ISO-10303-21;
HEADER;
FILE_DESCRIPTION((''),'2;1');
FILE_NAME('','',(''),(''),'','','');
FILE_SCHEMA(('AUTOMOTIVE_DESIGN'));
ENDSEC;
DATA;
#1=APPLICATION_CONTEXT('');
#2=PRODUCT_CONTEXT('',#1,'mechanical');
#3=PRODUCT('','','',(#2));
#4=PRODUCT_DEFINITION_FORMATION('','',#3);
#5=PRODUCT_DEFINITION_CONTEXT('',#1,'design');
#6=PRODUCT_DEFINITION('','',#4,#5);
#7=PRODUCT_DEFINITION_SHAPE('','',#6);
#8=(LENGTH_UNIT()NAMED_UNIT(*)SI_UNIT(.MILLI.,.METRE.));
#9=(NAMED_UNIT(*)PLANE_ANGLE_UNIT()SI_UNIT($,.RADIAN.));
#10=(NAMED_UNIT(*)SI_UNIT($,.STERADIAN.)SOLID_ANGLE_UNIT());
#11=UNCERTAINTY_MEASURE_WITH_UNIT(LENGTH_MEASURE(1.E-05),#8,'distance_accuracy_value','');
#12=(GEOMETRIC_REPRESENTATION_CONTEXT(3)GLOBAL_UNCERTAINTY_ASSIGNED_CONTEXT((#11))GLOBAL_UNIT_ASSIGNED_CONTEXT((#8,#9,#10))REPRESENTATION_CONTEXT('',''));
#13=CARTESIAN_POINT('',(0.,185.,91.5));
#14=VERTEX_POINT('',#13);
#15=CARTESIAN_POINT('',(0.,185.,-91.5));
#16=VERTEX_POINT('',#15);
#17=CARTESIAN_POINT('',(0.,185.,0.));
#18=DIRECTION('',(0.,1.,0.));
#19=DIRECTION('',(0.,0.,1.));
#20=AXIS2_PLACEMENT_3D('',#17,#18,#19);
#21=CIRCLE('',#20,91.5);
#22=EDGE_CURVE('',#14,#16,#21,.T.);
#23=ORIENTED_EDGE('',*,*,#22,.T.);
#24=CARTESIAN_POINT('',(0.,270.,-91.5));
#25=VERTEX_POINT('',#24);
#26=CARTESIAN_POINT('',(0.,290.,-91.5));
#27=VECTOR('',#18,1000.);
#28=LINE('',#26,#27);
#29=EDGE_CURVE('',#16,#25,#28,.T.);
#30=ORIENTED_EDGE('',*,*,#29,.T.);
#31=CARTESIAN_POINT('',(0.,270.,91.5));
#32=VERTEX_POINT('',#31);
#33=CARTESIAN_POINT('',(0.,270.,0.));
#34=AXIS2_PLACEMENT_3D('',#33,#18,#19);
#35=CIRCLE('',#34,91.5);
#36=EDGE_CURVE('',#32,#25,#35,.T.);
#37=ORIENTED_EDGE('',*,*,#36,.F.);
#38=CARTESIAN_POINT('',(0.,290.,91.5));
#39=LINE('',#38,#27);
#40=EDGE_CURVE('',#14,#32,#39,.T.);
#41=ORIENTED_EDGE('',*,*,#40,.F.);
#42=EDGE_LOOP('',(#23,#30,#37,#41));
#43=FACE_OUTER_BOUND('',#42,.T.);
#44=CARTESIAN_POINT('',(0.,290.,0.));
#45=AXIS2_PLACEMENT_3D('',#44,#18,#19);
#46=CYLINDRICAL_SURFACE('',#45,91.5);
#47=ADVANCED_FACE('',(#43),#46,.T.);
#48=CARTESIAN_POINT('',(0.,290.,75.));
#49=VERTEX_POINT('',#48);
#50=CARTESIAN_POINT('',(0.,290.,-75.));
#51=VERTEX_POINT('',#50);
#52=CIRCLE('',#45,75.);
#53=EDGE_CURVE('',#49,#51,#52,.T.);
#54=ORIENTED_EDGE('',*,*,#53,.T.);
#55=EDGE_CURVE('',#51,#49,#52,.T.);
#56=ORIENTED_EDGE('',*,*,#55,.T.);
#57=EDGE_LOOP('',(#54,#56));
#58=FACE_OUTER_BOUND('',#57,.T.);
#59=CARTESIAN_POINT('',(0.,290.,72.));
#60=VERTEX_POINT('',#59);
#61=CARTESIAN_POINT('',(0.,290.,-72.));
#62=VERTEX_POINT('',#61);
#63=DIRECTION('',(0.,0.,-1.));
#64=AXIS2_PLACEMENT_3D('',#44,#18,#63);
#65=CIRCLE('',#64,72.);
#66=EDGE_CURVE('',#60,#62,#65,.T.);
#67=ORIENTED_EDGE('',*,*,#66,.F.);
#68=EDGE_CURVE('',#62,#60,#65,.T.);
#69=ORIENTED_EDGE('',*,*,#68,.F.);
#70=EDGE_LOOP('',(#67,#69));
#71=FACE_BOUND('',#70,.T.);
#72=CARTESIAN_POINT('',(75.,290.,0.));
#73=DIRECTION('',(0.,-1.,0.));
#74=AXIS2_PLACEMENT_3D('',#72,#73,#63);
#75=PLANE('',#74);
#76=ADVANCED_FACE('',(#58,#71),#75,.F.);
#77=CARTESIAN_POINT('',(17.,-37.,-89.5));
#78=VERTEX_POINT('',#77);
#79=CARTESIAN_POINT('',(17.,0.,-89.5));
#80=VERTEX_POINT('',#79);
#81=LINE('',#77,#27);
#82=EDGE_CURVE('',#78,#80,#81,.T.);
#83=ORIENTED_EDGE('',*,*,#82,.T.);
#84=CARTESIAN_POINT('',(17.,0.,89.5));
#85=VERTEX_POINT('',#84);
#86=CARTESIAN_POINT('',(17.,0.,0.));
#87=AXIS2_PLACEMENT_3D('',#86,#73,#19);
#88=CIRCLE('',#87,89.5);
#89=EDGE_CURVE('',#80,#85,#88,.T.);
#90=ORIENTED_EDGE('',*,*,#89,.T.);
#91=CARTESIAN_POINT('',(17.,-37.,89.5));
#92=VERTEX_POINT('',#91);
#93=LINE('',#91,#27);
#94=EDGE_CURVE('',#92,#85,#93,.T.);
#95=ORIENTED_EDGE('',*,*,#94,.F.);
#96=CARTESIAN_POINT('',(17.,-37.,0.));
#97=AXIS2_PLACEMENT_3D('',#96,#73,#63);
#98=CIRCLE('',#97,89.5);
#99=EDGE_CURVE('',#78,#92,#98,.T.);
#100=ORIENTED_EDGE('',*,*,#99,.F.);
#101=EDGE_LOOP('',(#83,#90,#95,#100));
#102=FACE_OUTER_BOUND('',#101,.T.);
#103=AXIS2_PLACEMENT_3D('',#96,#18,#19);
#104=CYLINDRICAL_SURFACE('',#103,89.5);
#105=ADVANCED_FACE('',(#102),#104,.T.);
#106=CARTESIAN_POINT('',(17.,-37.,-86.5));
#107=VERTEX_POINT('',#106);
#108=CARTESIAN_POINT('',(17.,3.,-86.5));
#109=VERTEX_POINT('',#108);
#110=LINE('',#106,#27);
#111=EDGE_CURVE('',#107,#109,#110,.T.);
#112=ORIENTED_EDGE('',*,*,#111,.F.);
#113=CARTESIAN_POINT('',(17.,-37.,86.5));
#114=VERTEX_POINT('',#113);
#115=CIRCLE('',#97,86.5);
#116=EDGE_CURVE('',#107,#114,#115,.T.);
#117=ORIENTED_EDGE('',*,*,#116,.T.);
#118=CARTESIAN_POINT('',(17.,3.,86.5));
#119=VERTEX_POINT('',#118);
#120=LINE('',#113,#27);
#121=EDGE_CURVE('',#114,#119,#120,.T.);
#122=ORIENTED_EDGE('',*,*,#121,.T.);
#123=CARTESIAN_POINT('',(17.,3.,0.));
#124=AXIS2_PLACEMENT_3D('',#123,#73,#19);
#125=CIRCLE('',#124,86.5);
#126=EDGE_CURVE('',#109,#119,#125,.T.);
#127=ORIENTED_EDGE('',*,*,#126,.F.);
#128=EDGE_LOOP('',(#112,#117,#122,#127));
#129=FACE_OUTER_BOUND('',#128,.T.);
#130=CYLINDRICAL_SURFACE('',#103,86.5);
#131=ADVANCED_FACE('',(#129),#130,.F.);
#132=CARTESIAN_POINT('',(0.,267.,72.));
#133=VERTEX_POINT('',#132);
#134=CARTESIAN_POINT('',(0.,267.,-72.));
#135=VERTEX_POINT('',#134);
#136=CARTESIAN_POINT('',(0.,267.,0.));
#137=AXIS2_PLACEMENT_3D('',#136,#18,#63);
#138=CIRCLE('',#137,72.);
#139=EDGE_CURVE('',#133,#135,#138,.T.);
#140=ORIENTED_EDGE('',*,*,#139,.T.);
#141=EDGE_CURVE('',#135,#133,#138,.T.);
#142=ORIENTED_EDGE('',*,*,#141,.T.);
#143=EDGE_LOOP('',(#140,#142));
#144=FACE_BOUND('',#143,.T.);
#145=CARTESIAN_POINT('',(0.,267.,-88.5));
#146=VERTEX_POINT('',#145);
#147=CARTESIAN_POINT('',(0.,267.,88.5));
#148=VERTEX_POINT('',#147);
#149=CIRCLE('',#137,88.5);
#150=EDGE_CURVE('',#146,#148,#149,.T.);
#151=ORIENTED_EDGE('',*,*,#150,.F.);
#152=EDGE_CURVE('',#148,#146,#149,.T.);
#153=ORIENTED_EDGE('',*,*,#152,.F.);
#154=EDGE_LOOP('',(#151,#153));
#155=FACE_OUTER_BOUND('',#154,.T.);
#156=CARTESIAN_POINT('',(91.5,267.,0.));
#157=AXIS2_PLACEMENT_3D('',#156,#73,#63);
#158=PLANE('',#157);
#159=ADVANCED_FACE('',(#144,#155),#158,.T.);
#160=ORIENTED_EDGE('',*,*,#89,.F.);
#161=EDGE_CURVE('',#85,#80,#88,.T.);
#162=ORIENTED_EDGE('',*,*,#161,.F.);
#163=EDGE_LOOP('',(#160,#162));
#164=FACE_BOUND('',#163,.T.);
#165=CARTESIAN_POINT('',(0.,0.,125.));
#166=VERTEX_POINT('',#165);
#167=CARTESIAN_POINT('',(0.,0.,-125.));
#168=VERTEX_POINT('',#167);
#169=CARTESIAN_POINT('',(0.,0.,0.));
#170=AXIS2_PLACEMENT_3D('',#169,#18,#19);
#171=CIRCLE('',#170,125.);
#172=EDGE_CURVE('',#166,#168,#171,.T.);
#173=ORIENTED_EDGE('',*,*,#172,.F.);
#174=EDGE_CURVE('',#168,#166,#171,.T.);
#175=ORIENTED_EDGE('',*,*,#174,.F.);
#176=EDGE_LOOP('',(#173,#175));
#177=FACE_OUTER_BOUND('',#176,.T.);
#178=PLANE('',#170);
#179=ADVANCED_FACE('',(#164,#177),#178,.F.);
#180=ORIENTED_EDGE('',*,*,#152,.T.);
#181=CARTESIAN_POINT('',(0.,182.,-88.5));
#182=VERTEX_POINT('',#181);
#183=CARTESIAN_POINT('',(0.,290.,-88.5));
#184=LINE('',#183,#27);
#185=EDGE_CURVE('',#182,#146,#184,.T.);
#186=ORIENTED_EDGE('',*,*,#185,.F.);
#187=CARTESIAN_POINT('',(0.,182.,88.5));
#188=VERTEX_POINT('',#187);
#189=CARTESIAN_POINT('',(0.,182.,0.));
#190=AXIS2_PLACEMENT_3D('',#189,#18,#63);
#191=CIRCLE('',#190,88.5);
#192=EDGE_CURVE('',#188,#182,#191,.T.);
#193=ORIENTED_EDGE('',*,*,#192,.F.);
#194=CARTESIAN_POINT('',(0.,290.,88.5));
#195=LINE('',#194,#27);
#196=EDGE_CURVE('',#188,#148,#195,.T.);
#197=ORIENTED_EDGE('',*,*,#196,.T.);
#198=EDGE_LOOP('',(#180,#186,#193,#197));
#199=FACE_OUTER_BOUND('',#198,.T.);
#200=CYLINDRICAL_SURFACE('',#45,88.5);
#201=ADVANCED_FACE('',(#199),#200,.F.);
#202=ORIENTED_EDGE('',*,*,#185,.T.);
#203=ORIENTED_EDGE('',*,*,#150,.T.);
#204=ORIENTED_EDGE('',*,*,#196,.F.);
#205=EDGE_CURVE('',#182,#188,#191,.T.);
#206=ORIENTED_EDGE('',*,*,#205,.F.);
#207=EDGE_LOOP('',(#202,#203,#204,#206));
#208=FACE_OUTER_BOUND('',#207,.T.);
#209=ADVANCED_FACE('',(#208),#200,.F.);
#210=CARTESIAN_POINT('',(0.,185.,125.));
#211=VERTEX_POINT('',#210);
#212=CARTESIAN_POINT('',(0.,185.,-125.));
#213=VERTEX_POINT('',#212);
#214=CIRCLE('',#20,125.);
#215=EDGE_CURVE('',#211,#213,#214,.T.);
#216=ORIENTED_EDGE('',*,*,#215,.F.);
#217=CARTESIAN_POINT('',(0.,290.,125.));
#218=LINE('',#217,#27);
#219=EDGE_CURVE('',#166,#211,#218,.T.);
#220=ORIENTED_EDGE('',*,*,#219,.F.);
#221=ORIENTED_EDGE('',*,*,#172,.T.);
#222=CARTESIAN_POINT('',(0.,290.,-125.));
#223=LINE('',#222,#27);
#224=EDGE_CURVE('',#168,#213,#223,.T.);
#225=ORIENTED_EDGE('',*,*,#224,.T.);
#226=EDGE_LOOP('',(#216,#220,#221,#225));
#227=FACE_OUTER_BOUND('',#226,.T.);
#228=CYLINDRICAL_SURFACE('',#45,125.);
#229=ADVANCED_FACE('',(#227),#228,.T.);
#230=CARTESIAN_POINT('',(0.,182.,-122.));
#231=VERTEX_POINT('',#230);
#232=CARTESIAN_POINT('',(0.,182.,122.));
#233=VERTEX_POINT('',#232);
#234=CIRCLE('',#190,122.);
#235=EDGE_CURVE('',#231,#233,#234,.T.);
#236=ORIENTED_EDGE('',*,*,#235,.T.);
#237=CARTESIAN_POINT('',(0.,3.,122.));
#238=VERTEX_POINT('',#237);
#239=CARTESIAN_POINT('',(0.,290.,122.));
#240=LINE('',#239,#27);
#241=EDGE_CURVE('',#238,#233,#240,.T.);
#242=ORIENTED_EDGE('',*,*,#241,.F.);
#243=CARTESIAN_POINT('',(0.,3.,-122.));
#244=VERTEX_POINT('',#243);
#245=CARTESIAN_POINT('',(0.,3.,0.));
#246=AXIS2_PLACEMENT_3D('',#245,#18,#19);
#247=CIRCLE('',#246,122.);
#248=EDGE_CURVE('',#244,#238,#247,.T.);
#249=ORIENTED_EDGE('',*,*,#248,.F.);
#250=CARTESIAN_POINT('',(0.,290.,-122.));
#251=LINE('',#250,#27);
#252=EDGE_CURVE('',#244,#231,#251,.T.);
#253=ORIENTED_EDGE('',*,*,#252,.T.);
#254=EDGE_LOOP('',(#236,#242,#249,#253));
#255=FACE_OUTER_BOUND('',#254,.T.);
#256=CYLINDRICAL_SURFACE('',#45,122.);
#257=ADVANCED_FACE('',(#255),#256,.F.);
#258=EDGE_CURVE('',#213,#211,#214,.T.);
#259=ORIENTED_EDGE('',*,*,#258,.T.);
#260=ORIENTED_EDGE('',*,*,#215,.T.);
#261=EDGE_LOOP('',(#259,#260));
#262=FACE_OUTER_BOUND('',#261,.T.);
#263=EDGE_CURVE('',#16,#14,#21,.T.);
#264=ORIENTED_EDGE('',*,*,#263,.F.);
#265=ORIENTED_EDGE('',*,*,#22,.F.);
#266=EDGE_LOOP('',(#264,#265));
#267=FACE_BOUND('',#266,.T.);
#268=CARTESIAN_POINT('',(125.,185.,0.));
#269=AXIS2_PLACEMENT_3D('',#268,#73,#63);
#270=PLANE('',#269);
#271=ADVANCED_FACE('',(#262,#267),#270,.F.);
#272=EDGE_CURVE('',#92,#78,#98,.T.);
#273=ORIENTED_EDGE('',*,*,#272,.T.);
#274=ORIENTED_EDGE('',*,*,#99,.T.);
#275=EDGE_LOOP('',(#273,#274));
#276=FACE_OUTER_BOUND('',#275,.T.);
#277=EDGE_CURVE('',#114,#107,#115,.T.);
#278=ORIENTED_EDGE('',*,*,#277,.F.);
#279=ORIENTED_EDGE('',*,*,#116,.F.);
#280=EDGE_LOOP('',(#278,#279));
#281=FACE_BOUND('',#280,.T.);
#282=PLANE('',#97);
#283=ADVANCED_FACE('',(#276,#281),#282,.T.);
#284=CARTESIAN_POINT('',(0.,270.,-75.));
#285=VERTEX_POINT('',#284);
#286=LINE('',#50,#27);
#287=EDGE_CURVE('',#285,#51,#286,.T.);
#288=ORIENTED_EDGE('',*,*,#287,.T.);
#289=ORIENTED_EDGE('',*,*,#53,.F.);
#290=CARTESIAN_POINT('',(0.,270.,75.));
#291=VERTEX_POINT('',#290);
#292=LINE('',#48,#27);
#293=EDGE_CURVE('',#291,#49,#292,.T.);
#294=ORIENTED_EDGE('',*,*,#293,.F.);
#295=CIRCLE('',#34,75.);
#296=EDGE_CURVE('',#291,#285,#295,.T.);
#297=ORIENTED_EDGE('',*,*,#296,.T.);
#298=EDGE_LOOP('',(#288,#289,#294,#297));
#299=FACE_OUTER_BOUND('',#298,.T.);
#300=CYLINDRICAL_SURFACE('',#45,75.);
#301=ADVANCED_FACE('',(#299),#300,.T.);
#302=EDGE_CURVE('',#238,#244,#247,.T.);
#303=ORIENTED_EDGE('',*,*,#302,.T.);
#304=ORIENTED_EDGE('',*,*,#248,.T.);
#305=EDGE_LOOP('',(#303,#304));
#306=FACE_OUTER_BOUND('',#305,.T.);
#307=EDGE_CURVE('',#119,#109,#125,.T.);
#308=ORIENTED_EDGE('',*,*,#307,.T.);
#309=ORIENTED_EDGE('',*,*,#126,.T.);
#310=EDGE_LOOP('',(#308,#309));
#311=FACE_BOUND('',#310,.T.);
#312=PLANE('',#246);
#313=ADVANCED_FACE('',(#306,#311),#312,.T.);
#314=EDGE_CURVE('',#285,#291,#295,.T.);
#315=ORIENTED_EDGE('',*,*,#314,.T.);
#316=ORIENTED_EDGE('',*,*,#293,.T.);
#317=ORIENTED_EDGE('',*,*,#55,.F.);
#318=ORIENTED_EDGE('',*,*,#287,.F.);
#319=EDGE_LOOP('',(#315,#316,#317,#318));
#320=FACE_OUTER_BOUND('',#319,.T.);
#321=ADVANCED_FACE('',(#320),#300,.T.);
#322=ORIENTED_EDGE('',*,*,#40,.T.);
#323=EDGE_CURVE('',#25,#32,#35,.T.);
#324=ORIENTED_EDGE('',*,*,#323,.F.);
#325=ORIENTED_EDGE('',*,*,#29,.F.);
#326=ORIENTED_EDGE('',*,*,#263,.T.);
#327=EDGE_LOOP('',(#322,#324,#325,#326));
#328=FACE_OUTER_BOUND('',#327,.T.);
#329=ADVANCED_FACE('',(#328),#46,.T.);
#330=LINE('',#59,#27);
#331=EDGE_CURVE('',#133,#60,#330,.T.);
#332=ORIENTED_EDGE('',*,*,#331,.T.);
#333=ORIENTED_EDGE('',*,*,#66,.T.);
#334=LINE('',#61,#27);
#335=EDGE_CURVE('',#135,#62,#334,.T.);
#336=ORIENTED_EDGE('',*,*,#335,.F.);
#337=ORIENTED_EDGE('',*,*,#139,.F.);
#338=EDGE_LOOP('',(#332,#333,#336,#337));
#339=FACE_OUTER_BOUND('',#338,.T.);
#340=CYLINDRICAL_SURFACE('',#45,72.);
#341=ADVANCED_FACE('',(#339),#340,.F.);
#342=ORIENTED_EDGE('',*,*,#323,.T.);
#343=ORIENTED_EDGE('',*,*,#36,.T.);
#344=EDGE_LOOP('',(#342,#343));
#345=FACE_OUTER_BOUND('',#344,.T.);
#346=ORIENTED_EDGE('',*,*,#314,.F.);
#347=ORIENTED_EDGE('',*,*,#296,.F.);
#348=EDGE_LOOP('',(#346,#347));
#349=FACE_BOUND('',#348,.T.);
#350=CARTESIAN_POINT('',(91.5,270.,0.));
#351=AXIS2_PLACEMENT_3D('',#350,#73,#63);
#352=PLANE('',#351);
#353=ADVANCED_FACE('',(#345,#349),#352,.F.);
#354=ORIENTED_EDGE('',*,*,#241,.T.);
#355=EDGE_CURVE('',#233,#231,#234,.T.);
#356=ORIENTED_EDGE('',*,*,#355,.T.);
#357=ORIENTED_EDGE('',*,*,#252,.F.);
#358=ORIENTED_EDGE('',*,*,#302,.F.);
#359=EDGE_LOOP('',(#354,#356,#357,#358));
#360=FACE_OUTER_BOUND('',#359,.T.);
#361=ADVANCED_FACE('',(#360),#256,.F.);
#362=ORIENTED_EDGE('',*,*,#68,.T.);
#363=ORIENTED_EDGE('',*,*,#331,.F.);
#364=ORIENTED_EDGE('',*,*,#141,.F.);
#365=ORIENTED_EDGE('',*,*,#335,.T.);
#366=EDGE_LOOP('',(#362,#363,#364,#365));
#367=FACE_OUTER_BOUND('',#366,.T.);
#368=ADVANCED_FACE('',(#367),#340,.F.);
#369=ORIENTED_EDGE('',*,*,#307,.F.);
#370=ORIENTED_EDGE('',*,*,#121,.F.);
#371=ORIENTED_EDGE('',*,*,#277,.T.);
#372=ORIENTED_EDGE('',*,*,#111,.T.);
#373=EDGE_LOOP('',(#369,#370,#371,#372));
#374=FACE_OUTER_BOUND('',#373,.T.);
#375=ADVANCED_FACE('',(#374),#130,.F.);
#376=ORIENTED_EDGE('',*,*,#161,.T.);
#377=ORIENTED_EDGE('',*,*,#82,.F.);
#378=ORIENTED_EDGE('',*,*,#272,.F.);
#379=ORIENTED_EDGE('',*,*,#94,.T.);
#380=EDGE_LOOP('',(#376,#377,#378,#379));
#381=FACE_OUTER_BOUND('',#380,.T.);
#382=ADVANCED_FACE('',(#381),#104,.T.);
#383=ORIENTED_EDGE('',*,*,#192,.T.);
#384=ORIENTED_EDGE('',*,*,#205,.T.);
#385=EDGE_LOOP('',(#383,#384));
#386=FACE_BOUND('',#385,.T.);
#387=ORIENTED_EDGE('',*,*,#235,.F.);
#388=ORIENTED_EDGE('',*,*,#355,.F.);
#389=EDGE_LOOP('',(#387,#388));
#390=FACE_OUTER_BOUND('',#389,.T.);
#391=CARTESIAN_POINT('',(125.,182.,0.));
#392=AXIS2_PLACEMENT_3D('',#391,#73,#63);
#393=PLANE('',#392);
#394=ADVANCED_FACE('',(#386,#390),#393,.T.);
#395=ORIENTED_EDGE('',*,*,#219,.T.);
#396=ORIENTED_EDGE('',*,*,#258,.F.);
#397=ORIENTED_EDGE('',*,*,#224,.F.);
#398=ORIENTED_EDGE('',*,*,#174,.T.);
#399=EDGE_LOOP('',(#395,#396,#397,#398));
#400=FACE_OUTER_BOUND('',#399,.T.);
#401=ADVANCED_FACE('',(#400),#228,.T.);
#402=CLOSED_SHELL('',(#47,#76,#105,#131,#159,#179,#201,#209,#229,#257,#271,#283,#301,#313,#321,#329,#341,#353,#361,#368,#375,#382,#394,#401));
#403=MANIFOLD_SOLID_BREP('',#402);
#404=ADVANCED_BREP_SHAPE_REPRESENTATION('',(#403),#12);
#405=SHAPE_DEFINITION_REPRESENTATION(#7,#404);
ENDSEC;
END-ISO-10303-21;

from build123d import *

# Parameters (mm, degrees)
SKETCH2_R           = 89.5
BOSS_EXTRUDE1_DEPTH = 37
SHELL1_T            = -3


with BuildPart() as part:
    # Sketch1 → Revolve1 (revolve)
    with BuildSketch(Plane.XY, mode=Mode.PRIVATE) as revolve1_sk:
        Polygon((0, 0), (125, 0), (125, 185), (91.5, 185), (91.5, 270), (75, 270), (75, 290), (0, 290), align=None)
    revolve(revolve1_sk.sketch.rotate(Axis((0, 290, 0), (0, -1, 0)), 90), axis=Axis((0, 290, 0), (0, -1, 0)))

    # Sketch2 → Boss-Extrude1 (add)
    with BuildSketch(Plane.XZ):
        with Locations(Location((17, 0, 0), (0, 0, 90))):
            Circle(SKETCH2_R)
    extrude(amount=BOSS_EXTRUDE1_DEPTH)

    # Shell1
    shell1_openings = [part.faces().sort_by_distance(p)[0] for p in [
        (17, -37, 0),
        (0, 290, 0),
    ]]
    offset(amount=SHELL1_T, openings=shell1_openings, kind=Kind.INTERSECTION)


solid = part.part
